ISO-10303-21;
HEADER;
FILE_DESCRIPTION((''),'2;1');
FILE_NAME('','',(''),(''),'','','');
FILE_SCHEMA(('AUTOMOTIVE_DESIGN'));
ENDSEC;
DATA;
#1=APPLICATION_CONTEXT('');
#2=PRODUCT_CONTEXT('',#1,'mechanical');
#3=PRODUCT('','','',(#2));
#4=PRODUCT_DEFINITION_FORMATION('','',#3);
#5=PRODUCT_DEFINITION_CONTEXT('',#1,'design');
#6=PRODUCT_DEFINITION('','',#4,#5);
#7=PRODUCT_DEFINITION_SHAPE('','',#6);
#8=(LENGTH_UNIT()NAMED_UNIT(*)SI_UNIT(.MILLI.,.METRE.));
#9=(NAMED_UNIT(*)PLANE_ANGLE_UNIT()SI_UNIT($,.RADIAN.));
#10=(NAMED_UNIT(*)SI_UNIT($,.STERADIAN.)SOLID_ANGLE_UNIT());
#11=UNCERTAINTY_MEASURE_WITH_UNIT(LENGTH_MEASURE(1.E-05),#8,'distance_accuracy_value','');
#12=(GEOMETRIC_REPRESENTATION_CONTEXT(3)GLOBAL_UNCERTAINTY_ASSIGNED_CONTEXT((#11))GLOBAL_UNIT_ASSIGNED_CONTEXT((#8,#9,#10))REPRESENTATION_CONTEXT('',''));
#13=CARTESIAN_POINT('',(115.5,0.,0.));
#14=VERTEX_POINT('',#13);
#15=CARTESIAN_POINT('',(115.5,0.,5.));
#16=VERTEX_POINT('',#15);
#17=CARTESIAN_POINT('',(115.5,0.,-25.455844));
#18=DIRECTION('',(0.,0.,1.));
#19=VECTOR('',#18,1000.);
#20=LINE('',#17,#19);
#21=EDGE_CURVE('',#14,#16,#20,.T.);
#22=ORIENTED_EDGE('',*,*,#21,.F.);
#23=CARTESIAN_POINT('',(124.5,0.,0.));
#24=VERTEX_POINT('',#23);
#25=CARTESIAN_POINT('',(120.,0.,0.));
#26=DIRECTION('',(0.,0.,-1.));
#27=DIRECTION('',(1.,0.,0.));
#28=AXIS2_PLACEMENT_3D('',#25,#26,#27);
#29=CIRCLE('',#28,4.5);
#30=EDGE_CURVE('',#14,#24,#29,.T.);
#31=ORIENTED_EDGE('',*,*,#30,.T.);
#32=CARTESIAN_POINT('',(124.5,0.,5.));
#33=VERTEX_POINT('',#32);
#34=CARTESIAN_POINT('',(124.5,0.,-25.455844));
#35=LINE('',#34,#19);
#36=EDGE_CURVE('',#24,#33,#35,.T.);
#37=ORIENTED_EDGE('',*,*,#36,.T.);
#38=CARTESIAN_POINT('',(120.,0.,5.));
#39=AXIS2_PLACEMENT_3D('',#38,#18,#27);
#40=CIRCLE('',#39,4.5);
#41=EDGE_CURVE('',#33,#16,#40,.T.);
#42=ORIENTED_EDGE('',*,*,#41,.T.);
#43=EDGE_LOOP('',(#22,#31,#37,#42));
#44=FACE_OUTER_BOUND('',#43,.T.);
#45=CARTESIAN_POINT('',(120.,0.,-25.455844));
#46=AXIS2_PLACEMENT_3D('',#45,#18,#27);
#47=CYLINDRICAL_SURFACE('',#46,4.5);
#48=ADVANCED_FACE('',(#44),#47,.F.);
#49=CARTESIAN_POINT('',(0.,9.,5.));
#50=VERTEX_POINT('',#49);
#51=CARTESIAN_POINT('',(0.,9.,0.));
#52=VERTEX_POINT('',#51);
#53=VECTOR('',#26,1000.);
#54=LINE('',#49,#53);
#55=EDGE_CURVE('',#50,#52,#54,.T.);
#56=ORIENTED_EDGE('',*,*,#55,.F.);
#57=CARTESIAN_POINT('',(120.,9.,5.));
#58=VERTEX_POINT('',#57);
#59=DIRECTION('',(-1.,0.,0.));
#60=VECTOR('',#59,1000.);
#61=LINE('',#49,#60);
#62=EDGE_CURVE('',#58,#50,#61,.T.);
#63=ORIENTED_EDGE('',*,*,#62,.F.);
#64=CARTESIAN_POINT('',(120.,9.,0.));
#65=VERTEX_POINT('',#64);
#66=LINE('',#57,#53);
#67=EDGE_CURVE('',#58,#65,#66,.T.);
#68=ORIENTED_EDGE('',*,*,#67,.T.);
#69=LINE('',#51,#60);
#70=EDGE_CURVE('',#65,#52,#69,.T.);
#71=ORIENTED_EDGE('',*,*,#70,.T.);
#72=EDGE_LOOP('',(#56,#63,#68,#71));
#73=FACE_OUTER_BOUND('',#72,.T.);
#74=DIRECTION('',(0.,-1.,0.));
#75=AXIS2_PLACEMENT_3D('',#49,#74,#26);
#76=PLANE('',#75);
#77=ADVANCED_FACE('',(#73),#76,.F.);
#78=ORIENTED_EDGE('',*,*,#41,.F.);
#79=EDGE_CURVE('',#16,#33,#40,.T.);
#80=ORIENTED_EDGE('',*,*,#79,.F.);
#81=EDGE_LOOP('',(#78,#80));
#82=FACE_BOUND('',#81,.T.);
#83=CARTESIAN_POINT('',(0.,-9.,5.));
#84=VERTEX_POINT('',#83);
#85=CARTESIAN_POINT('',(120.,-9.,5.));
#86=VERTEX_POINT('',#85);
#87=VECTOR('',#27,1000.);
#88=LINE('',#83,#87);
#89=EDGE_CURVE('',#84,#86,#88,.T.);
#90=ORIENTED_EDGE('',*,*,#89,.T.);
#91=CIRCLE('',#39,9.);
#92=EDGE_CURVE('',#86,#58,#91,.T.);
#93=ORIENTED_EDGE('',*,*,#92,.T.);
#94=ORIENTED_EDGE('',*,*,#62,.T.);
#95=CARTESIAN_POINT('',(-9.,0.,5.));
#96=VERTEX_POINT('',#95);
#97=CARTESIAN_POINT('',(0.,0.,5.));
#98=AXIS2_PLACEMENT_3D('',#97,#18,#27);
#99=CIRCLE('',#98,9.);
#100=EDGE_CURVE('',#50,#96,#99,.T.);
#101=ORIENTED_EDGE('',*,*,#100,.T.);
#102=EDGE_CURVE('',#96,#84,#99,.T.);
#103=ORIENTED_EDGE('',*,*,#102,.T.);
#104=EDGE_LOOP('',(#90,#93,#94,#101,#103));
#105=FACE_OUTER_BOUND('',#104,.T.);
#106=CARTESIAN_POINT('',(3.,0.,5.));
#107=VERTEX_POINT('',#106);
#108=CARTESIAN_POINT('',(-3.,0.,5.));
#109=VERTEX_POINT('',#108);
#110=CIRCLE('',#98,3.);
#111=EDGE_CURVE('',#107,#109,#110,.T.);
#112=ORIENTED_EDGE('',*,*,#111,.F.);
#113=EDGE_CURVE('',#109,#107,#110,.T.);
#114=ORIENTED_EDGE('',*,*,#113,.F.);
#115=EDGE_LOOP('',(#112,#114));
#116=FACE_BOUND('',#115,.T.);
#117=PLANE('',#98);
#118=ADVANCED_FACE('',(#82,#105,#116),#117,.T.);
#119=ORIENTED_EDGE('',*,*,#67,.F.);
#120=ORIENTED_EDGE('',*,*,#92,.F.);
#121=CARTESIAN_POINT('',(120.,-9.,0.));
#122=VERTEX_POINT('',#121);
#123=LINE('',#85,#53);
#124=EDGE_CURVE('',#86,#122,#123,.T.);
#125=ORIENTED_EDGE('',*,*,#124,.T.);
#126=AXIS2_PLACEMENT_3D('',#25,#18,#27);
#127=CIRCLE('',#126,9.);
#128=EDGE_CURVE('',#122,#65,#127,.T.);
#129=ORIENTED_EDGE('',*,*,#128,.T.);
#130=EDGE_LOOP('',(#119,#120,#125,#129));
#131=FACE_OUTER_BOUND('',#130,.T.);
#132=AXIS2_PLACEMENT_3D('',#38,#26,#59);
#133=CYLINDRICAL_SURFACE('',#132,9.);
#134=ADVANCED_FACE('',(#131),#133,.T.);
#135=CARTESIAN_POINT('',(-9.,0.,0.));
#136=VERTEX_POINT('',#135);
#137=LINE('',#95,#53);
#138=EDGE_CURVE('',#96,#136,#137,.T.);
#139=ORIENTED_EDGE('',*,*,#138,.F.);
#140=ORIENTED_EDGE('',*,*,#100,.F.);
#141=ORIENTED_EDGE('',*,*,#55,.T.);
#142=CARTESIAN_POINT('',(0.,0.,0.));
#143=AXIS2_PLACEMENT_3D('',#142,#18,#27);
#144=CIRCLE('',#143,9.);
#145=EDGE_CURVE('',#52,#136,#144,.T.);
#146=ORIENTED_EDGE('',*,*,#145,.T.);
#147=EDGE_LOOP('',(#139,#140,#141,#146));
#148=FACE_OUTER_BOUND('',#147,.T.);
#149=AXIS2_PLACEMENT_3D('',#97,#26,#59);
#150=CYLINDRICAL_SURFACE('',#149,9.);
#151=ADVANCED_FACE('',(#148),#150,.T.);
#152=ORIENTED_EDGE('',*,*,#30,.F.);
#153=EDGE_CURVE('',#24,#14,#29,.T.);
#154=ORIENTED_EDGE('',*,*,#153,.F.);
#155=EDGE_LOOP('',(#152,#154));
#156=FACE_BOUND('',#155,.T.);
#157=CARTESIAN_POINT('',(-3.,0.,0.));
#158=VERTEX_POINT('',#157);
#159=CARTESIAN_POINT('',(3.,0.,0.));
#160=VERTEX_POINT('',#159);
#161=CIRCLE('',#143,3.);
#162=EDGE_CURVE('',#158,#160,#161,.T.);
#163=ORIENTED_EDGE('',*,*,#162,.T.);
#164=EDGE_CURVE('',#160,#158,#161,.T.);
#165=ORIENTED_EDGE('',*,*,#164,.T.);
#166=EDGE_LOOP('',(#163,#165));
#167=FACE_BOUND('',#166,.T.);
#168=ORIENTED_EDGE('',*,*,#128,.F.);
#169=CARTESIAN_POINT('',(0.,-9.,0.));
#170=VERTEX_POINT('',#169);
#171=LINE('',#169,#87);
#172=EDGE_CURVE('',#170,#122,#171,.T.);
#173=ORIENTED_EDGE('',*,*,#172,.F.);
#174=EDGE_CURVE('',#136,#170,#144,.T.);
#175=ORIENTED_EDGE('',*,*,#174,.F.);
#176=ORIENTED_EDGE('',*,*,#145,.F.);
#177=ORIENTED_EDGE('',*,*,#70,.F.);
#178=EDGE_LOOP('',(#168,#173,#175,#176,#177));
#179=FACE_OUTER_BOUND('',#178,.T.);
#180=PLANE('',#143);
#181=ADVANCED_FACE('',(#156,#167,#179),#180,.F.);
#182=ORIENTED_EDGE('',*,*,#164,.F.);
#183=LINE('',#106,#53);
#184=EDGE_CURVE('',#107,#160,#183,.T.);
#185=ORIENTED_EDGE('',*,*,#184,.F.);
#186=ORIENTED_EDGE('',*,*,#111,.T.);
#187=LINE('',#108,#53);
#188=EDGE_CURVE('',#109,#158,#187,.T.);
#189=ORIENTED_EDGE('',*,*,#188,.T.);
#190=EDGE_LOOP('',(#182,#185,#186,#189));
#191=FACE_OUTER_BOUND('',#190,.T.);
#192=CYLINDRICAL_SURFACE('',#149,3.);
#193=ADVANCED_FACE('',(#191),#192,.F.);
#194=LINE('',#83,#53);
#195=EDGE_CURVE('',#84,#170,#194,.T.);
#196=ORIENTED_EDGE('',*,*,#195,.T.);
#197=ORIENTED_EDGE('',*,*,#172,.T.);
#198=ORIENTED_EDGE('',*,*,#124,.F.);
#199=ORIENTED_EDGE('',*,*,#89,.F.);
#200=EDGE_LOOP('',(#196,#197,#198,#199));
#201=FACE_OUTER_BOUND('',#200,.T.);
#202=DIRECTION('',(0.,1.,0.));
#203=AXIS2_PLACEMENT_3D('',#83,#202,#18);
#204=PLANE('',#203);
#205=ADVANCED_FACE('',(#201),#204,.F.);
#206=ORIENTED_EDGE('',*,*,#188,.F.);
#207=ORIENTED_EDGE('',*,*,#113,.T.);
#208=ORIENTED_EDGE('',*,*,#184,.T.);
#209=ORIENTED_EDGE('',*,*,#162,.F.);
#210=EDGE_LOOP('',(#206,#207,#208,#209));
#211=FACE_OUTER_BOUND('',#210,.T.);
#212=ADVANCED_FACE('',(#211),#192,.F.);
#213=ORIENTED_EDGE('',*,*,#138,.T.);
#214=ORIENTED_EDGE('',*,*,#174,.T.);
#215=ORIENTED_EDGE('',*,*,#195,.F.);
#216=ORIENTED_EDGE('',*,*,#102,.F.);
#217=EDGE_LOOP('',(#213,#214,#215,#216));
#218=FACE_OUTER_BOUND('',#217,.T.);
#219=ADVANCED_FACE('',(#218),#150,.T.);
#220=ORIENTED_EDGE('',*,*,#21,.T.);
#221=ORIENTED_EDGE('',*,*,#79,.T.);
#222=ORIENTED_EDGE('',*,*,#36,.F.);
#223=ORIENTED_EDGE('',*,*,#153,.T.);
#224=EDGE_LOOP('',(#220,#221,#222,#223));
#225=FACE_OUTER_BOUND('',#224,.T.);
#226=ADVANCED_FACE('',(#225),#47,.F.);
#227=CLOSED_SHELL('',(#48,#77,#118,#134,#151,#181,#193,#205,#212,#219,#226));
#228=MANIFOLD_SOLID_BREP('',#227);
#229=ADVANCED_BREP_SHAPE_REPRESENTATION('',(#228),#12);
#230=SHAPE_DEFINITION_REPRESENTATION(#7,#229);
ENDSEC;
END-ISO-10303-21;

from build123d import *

# Parameters (mm, degrees)
SKETCH_1_R          = 3
EXTRUDE_1_DEPTH     = 5
SKETCH_3_R          = 6
CUT_EXTRUDE_1_DEPTH = 10
EXTRUDE_START       = -5
SKETCH_4_R          = 9
SKETCH_4_R_2        = 4.5
EXTRUDE_3_DEPTH     = 5


with BuildPart() as part:
    # 草图1 → 凸台-拉伸1 (new body)
    with BuildSketch(Plane.XY):
        with BuildLine():
            Line((0, 9), (120, 9))
            ThreePointArc((120, 9), (129, 0), (120, -9))
            Line((120, -9), (0, -9))
            ThreePointArc((0, -9), (-9, 0), (0, 9))
        make_face()
        Circle(SKETCH_1_R, mode=Mode.SUBTRACT)
        with Locations((120, 0)):
            Circle(SKETCH_1_R, mode=Mode.SUBTRACT)
    extrude(amount=EXTRUDE_1_DEPTH)

    # 草图3 → 切除-拉伸1 (cut)
    with BuildSketch(Plane.XY.offset(5)):
        with Locations((120, 0)):
            Circle(SKETCH_3_R)
    extrude(amount=-CUT_EXTRUDE_1_DEPTH, mode=Mode.SUBTRACT)

    # 草图4 → 凸台-拉伸3 (add)
    with BuildSketch(Plane.XY.offset(5).offset(EXTRUDE_START)):
        with Locations((120, 0)):
            Circle(SKETCH_4_R)
        with Locations((120, 0)):
            Circle(SKETCH_4_R_2, mode=Mode.SUBTRACT)
    extrude(amount=EXTRUDE_3_DEPTH)


solid = part.part
